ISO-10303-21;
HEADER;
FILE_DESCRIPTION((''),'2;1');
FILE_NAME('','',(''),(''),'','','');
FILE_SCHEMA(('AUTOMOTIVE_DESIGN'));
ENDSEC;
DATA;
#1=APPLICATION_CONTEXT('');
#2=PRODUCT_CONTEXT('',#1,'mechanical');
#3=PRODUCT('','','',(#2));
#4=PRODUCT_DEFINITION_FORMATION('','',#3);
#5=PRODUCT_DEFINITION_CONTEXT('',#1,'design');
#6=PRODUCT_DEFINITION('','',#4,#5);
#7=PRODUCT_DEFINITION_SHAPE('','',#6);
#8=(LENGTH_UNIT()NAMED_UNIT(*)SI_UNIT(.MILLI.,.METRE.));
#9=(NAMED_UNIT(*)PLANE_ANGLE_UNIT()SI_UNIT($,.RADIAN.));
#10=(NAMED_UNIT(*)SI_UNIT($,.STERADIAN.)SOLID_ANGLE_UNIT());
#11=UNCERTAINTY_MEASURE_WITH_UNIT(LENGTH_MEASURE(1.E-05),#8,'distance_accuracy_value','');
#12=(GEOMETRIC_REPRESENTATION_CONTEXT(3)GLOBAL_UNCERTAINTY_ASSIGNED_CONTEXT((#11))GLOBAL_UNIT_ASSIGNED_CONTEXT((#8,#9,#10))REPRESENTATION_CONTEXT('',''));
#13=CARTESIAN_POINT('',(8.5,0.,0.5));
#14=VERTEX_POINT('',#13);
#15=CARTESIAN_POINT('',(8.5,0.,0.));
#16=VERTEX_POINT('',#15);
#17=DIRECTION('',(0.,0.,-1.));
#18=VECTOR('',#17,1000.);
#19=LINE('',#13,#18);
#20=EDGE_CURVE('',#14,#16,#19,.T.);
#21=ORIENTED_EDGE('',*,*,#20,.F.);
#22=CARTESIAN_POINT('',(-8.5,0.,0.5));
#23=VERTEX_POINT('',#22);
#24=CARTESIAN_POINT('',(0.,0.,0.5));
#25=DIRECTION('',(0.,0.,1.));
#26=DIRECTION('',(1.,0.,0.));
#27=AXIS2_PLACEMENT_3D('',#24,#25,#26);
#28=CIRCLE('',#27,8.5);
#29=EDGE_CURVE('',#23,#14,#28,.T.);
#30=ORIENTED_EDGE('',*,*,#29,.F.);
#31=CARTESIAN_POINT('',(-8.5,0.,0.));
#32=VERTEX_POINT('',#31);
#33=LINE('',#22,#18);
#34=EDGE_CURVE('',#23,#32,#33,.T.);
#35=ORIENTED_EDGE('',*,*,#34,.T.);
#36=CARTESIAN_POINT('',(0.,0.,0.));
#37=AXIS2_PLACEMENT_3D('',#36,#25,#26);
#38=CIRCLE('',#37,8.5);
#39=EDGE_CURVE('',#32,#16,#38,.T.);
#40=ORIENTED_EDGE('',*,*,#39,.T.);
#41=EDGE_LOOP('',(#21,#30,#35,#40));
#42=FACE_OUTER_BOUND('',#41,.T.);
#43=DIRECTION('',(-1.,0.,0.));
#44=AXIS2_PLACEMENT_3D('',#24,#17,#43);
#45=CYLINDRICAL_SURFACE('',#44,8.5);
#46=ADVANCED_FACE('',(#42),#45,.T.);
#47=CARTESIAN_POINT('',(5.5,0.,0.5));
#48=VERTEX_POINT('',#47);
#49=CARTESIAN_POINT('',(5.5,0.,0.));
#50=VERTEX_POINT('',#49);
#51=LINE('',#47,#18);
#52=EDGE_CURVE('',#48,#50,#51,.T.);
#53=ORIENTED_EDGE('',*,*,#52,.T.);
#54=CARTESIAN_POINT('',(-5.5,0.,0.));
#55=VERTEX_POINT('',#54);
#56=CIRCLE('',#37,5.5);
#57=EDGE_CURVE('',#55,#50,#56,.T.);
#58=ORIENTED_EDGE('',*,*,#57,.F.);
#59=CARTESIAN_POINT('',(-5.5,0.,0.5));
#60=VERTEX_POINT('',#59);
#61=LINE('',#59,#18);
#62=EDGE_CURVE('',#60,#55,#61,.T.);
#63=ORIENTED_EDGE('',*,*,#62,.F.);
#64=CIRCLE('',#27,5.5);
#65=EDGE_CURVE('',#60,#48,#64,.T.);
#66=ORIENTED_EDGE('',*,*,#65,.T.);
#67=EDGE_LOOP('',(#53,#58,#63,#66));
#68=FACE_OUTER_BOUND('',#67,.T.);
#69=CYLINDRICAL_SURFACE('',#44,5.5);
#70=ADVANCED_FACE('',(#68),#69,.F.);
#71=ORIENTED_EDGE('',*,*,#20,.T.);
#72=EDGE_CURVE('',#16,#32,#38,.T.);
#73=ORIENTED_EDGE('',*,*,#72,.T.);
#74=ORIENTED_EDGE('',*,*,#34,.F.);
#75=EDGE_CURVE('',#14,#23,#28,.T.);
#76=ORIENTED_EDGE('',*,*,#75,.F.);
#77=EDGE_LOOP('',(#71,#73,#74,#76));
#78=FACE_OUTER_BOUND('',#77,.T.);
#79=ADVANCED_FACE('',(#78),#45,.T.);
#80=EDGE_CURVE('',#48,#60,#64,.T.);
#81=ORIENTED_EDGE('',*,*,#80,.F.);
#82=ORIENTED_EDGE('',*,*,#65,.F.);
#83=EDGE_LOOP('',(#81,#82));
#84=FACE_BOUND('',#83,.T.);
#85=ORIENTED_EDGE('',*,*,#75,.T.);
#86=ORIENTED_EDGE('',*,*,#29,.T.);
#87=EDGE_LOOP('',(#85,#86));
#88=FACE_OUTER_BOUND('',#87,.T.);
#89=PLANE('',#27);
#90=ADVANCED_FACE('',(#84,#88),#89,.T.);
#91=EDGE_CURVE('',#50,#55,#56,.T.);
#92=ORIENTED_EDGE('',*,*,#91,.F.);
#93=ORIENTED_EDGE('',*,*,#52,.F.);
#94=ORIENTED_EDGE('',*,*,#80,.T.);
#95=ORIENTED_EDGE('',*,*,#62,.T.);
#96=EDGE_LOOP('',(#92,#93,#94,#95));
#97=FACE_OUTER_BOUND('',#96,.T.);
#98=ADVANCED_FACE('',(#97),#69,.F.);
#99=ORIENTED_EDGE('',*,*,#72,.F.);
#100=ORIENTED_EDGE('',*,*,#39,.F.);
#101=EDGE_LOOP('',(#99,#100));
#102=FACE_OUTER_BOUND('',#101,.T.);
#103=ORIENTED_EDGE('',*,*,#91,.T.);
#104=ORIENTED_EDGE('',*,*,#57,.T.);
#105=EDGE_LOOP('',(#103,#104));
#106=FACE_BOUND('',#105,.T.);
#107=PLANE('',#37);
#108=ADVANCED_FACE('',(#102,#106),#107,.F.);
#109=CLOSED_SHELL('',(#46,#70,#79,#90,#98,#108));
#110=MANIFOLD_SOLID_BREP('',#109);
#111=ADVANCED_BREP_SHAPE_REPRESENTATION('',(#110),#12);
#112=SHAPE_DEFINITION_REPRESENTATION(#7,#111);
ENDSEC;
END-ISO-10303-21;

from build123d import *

# Parameters (mm, degrees)
SKETCH1_R           = 8.5
SKETCH1_R_2         = 5.5
BOSS_EXTRUDE1_DEPTH = 0.5


with BuildPart() as part:
    # Sketch1 → Boss-Extrude1 (new body)
    with BuildSketch(Plane.XY):
        Circle(SKETCH1_R)
        Circle(SKETCH1_R_2, mode=Mode.SUBTRACT)
    extrude(amount=BOSS_EXTRUDE1_DEPTH)


solid = part.part
